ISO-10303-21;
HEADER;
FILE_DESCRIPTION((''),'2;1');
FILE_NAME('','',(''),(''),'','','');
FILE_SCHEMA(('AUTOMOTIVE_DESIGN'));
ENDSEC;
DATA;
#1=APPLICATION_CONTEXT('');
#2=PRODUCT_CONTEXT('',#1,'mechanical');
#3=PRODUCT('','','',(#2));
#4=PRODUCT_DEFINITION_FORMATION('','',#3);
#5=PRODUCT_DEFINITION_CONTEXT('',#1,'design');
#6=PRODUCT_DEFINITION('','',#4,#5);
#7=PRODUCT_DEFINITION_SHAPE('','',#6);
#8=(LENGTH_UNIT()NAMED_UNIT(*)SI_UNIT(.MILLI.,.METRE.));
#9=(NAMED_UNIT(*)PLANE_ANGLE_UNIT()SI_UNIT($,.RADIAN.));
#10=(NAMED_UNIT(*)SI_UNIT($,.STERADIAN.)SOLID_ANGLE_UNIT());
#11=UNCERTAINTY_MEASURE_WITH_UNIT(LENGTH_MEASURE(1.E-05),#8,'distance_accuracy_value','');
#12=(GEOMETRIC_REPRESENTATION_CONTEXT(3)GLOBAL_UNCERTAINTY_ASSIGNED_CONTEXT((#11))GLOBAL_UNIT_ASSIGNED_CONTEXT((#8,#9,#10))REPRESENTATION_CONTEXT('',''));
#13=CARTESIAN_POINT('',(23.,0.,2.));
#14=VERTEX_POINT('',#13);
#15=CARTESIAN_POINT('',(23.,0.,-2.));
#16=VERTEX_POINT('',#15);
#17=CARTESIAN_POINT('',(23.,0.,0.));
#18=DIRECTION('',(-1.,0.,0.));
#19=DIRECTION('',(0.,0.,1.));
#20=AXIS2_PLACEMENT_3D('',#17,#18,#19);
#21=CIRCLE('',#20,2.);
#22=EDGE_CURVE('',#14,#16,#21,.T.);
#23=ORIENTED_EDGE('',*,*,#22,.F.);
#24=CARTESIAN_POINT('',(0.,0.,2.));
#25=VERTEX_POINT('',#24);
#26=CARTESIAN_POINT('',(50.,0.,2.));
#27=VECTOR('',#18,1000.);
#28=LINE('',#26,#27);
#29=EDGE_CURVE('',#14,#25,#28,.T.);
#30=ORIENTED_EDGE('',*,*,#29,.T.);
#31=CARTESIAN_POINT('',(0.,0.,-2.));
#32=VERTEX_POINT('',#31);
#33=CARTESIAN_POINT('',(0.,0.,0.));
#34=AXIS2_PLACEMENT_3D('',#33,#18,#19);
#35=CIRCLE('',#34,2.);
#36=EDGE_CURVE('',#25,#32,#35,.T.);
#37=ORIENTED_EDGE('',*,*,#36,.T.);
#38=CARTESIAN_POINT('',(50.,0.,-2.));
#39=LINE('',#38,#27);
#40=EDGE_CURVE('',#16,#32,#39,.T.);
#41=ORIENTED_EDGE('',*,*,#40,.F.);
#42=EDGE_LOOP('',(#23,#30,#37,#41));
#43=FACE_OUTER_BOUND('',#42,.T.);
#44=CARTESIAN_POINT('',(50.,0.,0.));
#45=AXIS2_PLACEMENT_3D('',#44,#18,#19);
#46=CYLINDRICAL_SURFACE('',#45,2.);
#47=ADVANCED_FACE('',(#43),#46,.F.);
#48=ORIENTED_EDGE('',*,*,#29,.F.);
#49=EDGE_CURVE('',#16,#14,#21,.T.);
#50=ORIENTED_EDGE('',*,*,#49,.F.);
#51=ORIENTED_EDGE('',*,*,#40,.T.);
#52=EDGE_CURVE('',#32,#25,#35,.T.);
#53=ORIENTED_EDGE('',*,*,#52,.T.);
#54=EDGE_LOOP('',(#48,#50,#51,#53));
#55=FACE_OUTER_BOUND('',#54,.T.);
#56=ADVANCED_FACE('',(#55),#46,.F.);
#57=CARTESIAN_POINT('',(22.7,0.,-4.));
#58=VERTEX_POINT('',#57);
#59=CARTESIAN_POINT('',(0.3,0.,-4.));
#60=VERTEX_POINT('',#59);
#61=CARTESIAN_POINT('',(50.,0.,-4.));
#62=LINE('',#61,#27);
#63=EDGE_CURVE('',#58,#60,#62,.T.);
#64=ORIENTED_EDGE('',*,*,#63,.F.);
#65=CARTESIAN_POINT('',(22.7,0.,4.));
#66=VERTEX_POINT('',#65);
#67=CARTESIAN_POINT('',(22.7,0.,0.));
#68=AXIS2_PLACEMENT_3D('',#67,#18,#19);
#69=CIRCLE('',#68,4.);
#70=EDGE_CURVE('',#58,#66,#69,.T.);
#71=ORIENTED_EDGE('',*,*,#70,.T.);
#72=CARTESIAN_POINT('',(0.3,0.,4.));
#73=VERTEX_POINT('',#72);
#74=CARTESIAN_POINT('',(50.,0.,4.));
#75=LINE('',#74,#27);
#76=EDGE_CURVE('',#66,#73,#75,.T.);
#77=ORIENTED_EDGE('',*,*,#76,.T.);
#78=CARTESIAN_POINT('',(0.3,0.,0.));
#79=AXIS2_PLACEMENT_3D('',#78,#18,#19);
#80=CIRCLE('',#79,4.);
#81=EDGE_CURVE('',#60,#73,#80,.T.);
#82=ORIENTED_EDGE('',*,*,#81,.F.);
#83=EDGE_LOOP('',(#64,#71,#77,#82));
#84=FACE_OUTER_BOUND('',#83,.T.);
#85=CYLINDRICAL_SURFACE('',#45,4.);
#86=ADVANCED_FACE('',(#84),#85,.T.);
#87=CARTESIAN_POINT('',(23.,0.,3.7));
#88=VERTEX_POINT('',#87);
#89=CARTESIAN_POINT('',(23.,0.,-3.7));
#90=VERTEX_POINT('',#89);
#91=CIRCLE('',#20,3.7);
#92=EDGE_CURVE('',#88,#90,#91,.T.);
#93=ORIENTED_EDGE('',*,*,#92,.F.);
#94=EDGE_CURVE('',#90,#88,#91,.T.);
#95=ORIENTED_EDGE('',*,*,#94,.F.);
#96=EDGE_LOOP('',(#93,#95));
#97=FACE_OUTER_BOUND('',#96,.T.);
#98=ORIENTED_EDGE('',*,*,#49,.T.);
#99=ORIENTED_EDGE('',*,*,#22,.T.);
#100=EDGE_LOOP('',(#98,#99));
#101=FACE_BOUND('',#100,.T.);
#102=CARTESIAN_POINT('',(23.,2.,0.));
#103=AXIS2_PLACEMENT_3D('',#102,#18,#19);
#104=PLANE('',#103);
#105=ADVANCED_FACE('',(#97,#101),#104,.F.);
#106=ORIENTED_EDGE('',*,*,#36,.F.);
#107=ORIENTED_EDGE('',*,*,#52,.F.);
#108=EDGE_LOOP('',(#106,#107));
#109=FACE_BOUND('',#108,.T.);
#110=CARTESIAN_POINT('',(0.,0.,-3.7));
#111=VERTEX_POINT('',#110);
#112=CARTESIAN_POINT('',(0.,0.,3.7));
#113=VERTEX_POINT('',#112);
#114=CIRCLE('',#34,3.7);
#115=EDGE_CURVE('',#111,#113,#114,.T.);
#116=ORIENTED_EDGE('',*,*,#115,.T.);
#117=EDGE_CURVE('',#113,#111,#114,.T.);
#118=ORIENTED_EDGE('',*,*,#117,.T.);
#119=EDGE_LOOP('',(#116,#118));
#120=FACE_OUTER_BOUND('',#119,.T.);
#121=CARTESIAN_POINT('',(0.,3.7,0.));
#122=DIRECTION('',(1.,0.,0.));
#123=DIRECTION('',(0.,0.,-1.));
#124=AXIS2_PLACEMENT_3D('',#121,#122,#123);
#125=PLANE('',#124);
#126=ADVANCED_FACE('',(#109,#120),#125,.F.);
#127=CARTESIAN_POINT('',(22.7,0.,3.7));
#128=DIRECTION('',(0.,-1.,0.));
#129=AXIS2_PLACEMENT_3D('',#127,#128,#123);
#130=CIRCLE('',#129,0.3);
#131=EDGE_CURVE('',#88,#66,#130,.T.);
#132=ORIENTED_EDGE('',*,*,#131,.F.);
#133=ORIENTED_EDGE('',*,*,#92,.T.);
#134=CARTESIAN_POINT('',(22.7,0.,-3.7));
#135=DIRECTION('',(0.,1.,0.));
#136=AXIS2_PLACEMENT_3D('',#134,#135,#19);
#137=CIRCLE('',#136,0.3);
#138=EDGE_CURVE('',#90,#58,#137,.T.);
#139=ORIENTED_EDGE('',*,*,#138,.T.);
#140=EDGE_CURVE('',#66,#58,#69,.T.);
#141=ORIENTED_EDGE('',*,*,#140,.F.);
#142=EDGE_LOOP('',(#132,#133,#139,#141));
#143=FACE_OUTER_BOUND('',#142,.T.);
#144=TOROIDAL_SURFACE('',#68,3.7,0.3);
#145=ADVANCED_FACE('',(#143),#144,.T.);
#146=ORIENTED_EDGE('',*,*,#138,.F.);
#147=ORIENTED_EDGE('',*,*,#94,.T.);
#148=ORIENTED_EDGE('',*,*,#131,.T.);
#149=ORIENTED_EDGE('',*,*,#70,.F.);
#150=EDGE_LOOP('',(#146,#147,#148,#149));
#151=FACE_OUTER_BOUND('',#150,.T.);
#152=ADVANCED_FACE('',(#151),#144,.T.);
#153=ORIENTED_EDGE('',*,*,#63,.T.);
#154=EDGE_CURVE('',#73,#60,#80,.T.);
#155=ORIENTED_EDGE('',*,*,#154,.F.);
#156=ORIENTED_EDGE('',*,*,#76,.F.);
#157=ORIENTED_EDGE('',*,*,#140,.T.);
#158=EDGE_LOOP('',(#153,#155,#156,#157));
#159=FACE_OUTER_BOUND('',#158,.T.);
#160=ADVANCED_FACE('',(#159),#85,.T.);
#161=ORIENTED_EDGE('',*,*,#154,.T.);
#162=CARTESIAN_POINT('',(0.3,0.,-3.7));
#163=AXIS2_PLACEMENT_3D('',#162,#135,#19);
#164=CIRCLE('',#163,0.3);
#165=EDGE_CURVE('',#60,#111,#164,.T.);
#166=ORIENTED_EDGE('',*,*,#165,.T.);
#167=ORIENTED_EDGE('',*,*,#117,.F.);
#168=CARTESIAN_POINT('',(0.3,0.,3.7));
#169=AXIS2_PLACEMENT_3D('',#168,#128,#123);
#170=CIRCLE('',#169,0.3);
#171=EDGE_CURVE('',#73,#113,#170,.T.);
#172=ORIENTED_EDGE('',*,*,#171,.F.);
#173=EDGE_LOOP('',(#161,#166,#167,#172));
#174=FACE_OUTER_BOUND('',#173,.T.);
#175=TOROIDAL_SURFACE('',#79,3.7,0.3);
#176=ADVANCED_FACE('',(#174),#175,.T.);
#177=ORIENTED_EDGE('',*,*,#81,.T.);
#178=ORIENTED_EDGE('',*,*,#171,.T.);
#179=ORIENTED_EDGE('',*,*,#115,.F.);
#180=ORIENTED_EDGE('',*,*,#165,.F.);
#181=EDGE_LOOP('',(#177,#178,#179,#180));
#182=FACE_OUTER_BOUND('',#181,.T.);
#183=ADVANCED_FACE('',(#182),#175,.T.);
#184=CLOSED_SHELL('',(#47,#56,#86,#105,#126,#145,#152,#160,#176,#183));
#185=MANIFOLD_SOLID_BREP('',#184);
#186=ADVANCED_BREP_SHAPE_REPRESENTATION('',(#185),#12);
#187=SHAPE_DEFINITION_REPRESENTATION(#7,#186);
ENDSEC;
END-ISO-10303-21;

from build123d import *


with BuildPart() as part:
    # Sketch1 → Revolve1 (revolve)
    with BuildSketch(Plane.XY, mode=Mode.PRIVATE) as revolve1_sk:
        with BuildLine():
            Line((0, 2), (23, 2))
            Line((23, 2), (23, 3.7))
            ThreePointArc((23, 3.7), (22.912132034, 3.912132034), (22.7, 4))
            Line((22.7, 4), (0.3, 4))
            ThreePointArc((0.3, 4), (0.087867966, 3.912132034), (0, 3.7))
            Line((0, 3.7), (0, 2))
        make_face()
    revolve(revolve1_sk.sketch.rotate(Axis((50, 0, 0), (-1, 0, 0)), 270), axis=Axis((50, 0, 0), (-1, 0, 0)))


solid = part.part
